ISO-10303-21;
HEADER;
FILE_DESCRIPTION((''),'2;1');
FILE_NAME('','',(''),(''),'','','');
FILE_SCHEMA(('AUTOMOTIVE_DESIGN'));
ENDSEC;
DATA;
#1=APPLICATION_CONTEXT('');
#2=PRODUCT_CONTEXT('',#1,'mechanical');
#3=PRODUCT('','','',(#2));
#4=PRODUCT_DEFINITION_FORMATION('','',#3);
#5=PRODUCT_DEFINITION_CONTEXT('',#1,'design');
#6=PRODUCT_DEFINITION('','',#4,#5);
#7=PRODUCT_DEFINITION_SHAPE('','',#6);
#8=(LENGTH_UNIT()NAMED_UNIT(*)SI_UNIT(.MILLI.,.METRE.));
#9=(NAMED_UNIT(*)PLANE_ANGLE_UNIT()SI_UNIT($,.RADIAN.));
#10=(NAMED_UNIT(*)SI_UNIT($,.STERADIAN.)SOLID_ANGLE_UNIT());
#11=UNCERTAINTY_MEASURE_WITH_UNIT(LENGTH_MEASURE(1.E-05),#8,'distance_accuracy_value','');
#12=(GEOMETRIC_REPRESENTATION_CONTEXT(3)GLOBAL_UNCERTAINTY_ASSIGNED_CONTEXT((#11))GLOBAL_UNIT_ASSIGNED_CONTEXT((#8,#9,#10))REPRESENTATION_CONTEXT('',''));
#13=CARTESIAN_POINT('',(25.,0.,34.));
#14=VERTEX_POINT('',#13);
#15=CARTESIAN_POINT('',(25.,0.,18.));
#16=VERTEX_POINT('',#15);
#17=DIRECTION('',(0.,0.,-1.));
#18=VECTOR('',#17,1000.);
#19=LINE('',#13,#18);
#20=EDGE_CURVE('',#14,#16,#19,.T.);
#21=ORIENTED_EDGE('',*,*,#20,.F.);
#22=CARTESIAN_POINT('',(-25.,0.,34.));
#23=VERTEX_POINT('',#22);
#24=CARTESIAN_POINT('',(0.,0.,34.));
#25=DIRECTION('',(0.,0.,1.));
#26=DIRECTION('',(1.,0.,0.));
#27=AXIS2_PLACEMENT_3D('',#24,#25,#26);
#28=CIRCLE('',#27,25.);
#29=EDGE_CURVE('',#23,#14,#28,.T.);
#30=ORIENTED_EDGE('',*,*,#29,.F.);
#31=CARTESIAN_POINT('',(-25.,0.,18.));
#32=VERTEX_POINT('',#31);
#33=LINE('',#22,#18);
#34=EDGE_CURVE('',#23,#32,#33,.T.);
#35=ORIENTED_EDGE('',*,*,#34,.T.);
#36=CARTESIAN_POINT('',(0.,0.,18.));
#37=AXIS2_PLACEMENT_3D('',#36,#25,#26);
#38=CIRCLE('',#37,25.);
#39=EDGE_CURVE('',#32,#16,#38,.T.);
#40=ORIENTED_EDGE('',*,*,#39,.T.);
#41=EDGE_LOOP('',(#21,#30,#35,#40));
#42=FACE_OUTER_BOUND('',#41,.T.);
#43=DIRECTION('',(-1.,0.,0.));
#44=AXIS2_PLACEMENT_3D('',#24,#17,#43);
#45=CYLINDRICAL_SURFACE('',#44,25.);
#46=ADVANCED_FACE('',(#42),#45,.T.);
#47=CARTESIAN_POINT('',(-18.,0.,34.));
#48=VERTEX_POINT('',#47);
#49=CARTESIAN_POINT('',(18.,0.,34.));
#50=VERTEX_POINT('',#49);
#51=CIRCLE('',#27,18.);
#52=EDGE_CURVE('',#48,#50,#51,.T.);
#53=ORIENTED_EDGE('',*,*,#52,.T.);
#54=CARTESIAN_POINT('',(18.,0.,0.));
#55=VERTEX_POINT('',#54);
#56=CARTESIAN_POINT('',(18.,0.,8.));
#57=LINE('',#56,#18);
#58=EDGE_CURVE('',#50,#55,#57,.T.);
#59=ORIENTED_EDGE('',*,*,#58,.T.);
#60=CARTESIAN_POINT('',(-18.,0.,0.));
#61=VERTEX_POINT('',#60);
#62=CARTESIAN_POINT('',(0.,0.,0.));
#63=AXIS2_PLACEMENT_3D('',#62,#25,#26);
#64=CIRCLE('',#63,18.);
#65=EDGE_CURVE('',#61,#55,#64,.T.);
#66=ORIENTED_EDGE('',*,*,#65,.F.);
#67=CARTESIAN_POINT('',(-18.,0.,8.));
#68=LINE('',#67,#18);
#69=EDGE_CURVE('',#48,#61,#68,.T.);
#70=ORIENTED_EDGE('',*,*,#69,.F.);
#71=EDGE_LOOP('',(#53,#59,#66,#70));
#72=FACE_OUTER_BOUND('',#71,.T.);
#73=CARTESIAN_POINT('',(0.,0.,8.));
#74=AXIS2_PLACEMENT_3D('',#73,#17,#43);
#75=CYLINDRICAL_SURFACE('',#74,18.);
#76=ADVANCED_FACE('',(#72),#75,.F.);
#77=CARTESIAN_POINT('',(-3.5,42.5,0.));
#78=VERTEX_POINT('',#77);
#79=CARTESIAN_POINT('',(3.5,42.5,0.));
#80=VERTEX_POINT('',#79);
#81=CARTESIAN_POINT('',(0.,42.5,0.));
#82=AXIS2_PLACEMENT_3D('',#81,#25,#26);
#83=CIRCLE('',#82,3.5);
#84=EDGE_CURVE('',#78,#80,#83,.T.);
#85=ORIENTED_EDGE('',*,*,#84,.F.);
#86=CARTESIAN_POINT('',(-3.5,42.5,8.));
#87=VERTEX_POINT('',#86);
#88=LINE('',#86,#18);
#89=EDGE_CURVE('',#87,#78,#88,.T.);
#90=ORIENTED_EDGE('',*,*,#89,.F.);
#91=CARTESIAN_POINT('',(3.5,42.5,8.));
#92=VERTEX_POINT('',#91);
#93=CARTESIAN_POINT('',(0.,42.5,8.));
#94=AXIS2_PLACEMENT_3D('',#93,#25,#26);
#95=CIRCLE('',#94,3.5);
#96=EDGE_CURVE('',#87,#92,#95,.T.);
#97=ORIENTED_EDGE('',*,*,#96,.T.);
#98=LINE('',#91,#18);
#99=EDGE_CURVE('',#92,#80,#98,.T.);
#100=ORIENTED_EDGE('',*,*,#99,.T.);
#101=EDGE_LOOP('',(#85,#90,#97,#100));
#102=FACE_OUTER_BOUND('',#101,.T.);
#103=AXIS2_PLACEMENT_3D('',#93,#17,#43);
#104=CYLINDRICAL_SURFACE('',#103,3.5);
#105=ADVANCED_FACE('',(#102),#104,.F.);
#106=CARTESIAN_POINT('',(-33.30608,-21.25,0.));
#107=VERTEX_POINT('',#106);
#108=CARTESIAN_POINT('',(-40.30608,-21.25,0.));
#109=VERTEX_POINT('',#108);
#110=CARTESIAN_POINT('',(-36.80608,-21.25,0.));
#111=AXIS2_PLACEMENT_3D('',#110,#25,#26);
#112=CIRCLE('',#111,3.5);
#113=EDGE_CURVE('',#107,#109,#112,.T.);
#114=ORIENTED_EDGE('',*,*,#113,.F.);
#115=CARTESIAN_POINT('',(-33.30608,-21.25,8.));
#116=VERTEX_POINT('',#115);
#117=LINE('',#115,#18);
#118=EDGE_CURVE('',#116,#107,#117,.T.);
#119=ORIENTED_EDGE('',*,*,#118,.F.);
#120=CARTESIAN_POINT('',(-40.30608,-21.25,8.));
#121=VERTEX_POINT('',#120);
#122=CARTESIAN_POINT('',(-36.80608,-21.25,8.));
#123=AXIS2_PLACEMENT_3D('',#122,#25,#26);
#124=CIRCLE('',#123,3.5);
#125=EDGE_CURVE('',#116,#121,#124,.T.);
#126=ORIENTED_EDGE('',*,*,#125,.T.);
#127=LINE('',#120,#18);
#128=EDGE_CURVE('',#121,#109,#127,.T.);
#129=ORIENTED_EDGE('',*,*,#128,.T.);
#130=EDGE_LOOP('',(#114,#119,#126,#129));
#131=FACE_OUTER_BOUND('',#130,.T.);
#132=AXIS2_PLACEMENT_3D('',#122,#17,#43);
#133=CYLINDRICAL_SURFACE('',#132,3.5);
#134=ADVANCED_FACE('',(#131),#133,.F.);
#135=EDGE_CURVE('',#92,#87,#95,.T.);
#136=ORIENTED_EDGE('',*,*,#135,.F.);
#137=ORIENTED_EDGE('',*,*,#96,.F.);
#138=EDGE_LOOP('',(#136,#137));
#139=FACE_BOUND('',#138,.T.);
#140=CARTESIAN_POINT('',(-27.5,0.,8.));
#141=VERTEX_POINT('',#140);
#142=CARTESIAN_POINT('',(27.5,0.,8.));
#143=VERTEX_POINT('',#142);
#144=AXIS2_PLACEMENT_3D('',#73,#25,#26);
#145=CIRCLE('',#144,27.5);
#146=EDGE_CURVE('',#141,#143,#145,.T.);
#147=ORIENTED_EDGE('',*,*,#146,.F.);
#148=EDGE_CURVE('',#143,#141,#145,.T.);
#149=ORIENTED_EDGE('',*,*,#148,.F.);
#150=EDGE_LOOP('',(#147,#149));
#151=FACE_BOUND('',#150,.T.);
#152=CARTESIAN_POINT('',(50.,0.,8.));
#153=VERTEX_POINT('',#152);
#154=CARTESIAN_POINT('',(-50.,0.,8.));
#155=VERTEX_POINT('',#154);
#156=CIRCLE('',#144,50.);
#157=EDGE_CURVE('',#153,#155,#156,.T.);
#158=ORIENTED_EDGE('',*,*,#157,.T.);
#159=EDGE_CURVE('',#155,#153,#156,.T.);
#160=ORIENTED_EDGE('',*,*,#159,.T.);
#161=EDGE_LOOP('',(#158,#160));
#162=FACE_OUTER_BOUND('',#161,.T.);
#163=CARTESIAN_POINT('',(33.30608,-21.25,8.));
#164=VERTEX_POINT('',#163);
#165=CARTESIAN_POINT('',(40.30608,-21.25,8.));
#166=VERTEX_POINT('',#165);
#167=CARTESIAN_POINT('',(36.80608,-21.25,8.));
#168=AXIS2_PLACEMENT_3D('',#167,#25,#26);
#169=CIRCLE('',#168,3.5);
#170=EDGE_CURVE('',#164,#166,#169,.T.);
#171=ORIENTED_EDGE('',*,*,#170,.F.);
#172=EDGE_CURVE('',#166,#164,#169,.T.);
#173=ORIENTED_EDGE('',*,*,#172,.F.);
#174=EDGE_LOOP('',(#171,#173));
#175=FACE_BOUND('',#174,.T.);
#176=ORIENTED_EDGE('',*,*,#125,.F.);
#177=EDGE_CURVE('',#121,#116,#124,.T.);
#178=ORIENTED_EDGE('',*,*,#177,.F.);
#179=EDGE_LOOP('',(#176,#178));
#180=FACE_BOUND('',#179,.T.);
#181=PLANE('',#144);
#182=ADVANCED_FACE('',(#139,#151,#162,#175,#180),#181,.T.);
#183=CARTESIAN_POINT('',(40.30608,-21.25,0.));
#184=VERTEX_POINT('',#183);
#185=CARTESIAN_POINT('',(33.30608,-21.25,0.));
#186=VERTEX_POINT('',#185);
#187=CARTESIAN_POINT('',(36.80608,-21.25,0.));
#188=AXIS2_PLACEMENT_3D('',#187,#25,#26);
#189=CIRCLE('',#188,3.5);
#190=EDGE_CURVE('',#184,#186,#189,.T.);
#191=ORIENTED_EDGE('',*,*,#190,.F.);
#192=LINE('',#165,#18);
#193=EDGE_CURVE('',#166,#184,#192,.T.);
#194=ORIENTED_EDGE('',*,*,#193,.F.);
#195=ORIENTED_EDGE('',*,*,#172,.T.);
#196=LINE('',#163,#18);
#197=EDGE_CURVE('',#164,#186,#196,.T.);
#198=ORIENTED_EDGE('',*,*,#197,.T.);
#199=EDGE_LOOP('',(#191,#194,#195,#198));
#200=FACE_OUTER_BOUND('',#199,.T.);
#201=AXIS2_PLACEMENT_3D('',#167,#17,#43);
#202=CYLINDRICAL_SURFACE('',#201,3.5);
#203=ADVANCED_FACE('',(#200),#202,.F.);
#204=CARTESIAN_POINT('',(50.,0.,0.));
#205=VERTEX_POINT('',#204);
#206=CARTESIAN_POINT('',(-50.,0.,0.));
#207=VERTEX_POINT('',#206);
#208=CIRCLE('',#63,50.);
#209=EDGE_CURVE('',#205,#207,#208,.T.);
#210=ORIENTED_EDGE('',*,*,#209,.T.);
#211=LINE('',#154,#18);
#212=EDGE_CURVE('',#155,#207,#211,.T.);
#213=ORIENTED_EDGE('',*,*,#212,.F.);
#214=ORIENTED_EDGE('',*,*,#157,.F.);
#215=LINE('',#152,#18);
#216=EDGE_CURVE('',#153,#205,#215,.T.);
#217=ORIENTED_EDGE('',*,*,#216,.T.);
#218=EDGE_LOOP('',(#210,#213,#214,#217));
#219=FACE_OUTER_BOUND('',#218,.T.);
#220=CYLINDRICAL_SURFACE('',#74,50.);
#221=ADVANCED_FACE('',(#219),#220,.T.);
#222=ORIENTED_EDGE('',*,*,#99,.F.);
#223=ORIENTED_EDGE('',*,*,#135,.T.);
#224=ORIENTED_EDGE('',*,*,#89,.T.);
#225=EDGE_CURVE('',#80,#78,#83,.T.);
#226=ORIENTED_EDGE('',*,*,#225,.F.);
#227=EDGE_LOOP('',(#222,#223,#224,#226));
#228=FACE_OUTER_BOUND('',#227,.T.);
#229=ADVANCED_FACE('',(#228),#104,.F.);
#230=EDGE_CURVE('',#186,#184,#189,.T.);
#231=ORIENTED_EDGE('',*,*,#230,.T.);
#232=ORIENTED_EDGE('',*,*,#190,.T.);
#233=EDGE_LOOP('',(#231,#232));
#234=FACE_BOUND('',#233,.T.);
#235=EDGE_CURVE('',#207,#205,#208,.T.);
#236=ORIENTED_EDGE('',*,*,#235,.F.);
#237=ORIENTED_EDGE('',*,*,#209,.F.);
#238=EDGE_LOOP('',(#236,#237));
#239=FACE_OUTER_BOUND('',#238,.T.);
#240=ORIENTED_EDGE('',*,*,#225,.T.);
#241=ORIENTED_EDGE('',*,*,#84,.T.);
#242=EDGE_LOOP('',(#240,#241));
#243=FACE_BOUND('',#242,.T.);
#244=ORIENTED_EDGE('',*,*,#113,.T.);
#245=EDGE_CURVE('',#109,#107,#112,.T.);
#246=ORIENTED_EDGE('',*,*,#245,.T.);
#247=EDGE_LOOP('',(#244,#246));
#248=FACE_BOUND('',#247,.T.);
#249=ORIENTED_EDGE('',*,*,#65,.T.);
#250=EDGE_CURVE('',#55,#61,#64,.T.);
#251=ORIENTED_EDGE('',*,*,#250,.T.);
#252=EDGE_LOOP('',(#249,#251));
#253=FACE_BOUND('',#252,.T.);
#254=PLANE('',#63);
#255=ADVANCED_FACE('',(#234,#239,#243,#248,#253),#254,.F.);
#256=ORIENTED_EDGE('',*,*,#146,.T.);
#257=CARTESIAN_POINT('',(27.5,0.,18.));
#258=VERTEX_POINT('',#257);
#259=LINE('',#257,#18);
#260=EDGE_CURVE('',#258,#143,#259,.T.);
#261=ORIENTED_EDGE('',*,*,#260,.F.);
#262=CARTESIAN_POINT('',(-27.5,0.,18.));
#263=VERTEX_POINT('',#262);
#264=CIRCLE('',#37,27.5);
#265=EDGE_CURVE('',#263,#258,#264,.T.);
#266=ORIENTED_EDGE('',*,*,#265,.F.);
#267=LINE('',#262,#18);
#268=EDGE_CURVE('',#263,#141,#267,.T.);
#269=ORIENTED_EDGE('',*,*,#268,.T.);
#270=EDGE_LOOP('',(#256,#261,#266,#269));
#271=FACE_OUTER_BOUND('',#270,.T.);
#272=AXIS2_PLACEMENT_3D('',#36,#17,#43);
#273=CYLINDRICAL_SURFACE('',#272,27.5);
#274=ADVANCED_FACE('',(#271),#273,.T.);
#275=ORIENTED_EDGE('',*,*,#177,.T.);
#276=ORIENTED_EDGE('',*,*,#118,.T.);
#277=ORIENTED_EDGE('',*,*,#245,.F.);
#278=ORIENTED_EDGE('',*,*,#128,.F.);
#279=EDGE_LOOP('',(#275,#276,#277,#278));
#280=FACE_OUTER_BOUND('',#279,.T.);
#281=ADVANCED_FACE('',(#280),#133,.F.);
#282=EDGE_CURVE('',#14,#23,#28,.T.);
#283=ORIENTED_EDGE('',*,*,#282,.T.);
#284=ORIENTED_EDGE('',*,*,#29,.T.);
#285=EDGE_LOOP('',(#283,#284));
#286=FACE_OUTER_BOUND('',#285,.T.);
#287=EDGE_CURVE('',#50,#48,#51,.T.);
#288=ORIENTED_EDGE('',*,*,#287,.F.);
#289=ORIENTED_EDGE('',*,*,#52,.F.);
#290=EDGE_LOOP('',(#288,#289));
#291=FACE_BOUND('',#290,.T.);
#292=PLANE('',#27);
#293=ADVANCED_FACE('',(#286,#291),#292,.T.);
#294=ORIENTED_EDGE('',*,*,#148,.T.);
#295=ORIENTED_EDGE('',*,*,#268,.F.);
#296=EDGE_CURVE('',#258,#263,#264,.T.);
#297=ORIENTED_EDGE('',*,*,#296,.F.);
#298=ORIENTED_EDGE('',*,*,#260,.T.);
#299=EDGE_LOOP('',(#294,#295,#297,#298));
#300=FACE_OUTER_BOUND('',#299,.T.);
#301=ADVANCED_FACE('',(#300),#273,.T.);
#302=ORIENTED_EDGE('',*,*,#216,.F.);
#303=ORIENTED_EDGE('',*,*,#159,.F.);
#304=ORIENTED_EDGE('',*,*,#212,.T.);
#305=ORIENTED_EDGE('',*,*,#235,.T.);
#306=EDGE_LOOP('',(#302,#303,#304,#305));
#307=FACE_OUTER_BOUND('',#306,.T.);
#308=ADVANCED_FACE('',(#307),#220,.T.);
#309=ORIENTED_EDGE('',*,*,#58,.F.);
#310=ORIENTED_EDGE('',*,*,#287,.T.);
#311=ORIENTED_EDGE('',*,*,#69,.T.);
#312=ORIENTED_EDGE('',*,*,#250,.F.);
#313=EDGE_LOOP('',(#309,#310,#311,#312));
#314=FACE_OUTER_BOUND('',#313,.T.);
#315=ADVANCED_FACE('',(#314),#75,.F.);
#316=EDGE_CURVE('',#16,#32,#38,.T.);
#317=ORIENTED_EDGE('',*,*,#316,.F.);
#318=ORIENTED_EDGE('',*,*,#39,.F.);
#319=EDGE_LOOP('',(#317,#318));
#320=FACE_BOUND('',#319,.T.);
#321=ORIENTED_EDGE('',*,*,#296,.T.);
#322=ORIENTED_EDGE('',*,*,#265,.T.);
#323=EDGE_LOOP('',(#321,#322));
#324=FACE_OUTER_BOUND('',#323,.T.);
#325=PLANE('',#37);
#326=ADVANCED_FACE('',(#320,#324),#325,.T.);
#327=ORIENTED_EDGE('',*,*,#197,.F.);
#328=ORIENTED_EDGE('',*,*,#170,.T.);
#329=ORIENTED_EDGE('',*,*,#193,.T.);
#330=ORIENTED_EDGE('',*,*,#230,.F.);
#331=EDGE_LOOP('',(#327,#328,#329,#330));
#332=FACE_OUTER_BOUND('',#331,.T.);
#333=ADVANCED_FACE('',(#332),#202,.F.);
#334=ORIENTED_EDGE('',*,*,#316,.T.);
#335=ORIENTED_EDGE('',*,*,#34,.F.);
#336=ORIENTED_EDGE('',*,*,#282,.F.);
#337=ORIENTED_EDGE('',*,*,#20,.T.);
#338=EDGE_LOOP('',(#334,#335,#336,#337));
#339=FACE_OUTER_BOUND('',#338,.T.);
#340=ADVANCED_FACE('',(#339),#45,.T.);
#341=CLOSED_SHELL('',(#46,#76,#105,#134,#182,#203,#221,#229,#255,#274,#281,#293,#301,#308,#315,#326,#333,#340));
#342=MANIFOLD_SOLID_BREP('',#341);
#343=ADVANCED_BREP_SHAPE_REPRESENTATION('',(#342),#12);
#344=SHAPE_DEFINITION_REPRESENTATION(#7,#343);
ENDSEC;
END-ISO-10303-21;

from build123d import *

# Parameters (mm, degrees)
SKETCH1_R           = 50
SKETCH1_R_2         = 3.5
SKETCH1_R_3         = 18
BOSS_EXTRUDE1_DEPTH = 8
SKETCH2_R           = 27.5
SKETCH2_R_2         = 18
BOSS_EXTRUDE2_DEPTH = 10
SKETCH3_R           = 25
SKETCH3_R_2         = 18
BOSS_EXTRUDE3_DEPTH = 16


with BuildPart() as part:
    # Sketch1 → Boss-Extrude1 (new body)
    with BuildSketch(Plane.XY):
        Circle(SKETCH1_R)
        with Locations((0, 42.5)):
            Circle(SKETCH1_R_2, mode=Mode.SUBTRACT)
        with Locations((-36.806079661, -21.25)):
            Circle(SKETCH1_R_2, mode=Mode.SUBTRACT)
        with Locations((36.806079661, -21.25)):
            Circle(SKETCH1_R_2, mode=Mode.SUBTRACT)
        Circle(SKETCH1_R_3, mode=Mode.SUBTRACT)
    extrude(amount=BOSS_EXTRUDE1_DEPTH)

    # Sketch2 → Boss-Extrude2 (add)
    with BuildSketch(Plane.XY.offset(8)):
        Circle(SKETCH2_R)
        Circle(SKETCH2_R_2, mode=Mode.SUBTRACT)
    extrude(amount=BOSS_EXTRUDE2_DEPTH)

    # Sketch3 → Boss-Extrude3 (add)
    with BuildSketch(Plane.XY.offset(18)):
        Circle(SKETCH3_R)
        Circle(SKETCH3_R_2, mode=Mode.SUBTRACT)
    extrude(amount=BOSS_EXTRUDE3_DEPTH)


solid = part.part
